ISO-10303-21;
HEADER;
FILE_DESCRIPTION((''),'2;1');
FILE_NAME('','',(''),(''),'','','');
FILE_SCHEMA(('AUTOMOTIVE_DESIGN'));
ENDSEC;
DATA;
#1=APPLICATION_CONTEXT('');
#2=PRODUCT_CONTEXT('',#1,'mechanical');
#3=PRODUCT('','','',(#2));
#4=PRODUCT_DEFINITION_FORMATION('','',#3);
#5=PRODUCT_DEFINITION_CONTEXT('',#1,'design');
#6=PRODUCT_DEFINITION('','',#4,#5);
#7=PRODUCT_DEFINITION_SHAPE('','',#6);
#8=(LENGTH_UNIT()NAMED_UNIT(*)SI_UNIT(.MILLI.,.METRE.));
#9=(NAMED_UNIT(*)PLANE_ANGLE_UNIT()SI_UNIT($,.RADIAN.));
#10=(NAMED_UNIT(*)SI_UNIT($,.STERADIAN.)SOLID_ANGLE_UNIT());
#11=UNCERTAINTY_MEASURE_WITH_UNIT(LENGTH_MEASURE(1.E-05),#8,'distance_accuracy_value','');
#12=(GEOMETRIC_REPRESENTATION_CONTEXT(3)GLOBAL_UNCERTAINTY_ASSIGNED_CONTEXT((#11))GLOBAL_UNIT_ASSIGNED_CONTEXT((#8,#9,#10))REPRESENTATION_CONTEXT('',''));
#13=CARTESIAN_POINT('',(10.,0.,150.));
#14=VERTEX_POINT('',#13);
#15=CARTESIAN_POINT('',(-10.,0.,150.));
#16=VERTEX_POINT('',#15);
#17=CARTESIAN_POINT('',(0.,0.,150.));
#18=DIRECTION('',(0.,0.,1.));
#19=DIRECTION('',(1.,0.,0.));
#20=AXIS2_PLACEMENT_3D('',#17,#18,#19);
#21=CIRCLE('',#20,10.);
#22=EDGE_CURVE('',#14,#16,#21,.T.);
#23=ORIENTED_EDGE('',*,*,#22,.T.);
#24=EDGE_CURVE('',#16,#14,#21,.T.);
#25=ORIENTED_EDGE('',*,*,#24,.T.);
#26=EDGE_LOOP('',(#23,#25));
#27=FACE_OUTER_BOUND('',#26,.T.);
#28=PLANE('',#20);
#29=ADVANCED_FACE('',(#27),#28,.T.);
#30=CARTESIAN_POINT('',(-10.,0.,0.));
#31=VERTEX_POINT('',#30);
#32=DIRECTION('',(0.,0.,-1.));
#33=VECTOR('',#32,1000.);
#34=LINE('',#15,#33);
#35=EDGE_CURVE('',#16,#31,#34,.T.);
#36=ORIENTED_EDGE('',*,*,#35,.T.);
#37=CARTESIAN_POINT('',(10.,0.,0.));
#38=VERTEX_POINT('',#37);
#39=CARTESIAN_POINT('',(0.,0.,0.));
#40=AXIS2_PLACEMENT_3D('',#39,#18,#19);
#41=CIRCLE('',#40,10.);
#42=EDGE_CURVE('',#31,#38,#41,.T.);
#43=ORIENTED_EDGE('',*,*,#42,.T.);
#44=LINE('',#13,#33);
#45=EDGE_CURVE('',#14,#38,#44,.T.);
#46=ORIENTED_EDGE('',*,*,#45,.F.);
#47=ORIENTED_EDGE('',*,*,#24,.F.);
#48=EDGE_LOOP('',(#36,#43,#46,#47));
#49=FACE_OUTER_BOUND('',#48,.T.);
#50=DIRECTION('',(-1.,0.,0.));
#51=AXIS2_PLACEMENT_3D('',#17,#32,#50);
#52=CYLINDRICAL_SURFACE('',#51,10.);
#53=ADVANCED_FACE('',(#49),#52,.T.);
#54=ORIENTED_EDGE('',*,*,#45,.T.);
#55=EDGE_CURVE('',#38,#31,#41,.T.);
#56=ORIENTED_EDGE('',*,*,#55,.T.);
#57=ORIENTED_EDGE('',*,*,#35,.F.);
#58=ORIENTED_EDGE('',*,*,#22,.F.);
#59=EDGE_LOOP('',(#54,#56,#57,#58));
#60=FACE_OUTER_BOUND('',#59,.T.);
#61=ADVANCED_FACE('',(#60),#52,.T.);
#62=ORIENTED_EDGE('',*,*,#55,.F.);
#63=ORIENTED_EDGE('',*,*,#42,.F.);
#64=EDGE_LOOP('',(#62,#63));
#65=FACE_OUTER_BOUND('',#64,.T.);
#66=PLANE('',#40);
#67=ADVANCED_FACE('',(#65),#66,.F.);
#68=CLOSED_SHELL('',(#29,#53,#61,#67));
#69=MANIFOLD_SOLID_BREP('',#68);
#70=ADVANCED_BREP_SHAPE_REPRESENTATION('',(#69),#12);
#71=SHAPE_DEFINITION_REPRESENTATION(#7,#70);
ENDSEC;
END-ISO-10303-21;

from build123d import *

# Parameters (mm, degrees)
SKETCH1_R           = 10
BOSS_EXTRUDE1_DEPTH = 150


with BuildPart() as part:
    # Sketch1 → Boss-Extrude1 (new body)
    with BuildSketch(Plane.XY):
        Circle(SKETCH1_R)
    extrude(amount=BOSS_EXTRUDE1_DEPTH)


solid = part.part
